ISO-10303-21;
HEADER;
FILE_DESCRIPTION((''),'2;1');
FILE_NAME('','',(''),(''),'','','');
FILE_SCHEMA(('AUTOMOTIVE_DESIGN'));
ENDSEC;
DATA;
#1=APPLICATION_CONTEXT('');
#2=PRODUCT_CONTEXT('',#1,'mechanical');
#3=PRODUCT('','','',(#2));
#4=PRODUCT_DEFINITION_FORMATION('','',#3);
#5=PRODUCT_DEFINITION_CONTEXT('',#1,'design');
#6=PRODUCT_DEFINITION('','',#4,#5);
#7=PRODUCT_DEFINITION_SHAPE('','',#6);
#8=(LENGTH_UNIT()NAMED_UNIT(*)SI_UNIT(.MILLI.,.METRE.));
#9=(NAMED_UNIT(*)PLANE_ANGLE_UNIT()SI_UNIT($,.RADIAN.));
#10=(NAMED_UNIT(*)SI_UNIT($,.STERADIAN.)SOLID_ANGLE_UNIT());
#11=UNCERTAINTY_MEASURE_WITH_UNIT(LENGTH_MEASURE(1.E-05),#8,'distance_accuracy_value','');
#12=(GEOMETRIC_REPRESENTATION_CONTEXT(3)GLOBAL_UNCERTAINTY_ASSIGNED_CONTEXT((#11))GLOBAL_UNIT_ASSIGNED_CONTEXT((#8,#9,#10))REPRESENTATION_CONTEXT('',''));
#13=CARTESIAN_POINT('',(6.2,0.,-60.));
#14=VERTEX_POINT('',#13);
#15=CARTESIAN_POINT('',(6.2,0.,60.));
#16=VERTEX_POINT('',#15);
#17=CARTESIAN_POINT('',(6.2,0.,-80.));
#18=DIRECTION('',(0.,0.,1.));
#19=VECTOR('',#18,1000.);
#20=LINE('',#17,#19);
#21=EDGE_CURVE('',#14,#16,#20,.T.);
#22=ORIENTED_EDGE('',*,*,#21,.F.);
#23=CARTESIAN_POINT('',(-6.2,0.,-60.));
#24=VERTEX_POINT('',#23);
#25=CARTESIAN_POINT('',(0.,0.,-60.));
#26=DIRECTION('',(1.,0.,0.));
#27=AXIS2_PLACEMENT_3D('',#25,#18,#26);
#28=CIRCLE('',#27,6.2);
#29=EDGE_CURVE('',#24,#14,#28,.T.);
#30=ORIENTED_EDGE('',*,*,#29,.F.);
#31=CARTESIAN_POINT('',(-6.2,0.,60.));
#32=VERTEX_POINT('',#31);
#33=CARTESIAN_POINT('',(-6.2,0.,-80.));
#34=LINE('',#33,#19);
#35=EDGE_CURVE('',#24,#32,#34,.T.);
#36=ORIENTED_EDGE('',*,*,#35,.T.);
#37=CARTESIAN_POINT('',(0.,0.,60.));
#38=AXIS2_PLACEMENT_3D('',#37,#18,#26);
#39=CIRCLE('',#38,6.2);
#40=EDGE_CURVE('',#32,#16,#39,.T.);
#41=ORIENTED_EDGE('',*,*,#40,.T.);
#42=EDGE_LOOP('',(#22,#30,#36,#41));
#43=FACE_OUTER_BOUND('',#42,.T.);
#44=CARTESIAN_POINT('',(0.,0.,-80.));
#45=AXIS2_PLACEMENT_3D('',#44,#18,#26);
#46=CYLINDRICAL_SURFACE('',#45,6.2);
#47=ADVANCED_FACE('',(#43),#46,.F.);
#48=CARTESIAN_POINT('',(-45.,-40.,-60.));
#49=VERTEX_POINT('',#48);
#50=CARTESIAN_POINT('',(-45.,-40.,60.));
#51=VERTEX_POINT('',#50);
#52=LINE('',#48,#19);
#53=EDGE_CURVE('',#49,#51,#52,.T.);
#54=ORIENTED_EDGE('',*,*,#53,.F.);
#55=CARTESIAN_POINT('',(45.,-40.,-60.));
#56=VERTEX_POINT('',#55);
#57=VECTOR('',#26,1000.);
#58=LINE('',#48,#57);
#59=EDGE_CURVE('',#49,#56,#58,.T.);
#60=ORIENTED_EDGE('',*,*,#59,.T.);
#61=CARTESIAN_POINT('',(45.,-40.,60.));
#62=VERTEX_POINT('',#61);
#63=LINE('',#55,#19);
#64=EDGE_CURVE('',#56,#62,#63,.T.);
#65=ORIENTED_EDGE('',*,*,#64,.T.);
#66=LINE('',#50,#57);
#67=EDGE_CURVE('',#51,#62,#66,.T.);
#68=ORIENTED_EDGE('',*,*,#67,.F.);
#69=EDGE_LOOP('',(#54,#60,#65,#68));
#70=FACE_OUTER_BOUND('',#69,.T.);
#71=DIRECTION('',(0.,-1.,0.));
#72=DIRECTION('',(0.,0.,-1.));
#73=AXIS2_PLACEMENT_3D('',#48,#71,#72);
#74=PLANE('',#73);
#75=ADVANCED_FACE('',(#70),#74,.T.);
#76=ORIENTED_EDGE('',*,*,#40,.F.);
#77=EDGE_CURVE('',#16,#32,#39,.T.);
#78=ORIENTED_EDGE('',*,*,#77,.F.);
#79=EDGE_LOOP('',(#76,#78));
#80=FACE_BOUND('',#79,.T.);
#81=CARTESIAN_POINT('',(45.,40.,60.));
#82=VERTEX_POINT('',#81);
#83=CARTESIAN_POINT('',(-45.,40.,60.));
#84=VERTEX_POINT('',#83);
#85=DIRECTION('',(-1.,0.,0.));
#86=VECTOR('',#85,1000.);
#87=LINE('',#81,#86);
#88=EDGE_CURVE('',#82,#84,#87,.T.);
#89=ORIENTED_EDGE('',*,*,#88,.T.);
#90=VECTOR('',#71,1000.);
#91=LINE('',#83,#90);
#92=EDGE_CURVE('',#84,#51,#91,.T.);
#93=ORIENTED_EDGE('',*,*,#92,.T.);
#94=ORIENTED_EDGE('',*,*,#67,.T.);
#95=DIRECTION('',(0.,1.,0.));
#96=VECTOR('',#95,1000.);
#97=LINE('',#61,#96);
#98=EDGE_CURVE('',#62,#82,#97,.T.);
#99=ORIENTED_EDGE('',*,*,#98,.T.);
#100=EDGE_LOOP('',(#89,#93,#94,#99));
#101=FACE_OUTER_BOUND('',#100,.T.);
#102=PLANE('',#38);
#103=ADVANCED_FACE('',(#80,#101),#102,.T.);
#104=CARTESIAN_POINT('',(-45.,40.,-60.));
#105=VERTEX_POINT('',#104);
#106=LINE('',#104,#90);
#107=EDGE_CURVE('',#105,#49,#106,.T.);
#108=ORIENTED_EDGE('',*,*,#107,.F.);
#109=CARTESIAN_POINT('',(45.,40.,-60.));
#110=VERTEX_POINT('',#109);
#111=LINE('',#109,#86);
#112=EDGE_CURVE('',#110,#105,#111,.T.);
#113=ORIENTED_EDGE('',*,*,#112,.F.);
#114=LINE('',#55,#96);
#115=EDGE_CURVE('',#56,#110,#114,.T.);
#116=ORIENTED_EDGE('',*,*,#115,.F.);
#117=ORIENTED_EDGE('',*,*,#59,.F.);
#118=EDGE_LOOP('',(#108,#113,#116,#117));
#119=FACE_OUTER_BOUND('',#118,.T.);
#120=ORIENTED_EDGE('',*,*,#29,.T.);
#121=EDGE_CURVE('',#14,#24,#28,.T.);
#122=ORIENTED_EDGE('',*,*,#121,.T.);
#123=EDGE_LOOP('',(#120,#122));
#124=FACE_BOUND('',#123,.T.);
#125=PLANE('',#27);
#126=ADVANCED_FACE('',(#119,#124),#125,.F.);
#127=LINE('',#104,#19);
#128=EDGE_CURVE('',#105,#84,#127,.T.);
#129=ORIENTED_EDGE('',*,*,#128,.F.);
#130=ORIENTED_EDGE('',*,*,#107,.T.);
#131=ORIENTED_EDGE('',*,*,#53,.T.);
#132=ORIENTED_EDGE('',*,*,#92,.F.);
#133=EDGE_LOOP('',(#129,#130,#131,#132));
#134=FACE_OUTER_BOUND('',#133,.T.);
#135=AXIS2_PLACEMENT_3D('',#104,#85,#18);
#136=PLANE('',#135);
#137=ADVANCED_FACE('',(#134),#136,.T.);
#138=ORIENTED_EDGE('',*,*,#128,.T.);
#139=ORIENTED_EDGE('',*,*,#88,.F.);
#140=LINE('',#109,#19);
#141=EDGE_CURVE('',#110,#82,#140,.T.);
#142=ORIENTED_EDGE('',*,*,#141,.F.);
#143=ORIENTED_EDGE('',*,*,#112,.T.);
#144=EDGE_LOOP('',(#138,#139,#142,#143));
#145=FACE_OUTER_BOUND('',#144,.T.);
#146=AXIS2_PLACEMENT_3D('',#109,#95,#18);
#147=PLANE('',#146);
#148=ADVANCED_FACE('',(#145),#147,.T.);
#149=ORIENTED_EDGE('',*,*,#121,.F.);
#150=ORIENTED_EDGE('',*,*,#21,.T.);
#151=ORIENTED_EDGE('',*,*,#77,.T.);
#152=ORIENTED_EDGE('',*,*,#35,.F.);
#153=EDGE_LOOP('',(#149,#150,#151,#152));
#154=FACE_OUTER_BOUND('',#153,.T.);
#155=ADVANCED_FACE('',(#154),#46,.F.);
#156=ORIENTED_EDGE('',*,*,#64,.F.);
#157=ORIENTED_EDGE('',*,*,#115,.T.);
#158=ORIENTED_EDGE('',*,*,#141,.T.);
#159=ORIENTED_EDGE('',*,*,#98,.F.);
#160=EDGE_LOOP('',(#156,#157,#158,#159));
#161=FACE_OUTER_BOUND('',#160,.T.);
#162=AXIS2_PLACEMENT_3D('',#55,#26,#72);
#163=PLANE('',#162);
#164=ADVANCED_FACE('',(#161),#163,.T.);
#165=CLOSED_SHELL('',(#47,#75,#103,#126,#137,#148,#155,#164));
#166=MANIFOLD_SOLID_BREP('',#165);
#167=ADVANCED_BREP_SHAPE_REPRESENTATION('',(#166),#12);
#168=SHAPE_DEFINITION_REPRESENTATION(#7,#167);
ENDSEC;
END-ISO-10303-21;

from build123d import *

# Parameters (mm, degrees)
SKETCH_1_W          = 90
SKETCH_1_H          = 80
EXTRUDE_1_DEPTH     = 60
SKETCH_2_R          = 6.2
CUT_EXTRUDE_1_DEPTH = 80


with BuildPart() as part:
    # 草图1 → 凸台-拉伸1 (new, symmetric)
    with BuildSketch(Plane.XY):
        Rectangle(SKETCH_1_W, SKETCH_1_H)
    extrude(amount=EXTRUDE_1_DEPTH, both=True)

    # 草图2 → 切除-拉伸1 (cut, symmetric)
    with BuildSketch(Plane.XY):
        Circle(SKETCH_2_R)
    extrude(amount=CUT_EXTRUDE_1_DEPTH, both=True, mode=Mode.SUBTRACT)


solid = part.part
